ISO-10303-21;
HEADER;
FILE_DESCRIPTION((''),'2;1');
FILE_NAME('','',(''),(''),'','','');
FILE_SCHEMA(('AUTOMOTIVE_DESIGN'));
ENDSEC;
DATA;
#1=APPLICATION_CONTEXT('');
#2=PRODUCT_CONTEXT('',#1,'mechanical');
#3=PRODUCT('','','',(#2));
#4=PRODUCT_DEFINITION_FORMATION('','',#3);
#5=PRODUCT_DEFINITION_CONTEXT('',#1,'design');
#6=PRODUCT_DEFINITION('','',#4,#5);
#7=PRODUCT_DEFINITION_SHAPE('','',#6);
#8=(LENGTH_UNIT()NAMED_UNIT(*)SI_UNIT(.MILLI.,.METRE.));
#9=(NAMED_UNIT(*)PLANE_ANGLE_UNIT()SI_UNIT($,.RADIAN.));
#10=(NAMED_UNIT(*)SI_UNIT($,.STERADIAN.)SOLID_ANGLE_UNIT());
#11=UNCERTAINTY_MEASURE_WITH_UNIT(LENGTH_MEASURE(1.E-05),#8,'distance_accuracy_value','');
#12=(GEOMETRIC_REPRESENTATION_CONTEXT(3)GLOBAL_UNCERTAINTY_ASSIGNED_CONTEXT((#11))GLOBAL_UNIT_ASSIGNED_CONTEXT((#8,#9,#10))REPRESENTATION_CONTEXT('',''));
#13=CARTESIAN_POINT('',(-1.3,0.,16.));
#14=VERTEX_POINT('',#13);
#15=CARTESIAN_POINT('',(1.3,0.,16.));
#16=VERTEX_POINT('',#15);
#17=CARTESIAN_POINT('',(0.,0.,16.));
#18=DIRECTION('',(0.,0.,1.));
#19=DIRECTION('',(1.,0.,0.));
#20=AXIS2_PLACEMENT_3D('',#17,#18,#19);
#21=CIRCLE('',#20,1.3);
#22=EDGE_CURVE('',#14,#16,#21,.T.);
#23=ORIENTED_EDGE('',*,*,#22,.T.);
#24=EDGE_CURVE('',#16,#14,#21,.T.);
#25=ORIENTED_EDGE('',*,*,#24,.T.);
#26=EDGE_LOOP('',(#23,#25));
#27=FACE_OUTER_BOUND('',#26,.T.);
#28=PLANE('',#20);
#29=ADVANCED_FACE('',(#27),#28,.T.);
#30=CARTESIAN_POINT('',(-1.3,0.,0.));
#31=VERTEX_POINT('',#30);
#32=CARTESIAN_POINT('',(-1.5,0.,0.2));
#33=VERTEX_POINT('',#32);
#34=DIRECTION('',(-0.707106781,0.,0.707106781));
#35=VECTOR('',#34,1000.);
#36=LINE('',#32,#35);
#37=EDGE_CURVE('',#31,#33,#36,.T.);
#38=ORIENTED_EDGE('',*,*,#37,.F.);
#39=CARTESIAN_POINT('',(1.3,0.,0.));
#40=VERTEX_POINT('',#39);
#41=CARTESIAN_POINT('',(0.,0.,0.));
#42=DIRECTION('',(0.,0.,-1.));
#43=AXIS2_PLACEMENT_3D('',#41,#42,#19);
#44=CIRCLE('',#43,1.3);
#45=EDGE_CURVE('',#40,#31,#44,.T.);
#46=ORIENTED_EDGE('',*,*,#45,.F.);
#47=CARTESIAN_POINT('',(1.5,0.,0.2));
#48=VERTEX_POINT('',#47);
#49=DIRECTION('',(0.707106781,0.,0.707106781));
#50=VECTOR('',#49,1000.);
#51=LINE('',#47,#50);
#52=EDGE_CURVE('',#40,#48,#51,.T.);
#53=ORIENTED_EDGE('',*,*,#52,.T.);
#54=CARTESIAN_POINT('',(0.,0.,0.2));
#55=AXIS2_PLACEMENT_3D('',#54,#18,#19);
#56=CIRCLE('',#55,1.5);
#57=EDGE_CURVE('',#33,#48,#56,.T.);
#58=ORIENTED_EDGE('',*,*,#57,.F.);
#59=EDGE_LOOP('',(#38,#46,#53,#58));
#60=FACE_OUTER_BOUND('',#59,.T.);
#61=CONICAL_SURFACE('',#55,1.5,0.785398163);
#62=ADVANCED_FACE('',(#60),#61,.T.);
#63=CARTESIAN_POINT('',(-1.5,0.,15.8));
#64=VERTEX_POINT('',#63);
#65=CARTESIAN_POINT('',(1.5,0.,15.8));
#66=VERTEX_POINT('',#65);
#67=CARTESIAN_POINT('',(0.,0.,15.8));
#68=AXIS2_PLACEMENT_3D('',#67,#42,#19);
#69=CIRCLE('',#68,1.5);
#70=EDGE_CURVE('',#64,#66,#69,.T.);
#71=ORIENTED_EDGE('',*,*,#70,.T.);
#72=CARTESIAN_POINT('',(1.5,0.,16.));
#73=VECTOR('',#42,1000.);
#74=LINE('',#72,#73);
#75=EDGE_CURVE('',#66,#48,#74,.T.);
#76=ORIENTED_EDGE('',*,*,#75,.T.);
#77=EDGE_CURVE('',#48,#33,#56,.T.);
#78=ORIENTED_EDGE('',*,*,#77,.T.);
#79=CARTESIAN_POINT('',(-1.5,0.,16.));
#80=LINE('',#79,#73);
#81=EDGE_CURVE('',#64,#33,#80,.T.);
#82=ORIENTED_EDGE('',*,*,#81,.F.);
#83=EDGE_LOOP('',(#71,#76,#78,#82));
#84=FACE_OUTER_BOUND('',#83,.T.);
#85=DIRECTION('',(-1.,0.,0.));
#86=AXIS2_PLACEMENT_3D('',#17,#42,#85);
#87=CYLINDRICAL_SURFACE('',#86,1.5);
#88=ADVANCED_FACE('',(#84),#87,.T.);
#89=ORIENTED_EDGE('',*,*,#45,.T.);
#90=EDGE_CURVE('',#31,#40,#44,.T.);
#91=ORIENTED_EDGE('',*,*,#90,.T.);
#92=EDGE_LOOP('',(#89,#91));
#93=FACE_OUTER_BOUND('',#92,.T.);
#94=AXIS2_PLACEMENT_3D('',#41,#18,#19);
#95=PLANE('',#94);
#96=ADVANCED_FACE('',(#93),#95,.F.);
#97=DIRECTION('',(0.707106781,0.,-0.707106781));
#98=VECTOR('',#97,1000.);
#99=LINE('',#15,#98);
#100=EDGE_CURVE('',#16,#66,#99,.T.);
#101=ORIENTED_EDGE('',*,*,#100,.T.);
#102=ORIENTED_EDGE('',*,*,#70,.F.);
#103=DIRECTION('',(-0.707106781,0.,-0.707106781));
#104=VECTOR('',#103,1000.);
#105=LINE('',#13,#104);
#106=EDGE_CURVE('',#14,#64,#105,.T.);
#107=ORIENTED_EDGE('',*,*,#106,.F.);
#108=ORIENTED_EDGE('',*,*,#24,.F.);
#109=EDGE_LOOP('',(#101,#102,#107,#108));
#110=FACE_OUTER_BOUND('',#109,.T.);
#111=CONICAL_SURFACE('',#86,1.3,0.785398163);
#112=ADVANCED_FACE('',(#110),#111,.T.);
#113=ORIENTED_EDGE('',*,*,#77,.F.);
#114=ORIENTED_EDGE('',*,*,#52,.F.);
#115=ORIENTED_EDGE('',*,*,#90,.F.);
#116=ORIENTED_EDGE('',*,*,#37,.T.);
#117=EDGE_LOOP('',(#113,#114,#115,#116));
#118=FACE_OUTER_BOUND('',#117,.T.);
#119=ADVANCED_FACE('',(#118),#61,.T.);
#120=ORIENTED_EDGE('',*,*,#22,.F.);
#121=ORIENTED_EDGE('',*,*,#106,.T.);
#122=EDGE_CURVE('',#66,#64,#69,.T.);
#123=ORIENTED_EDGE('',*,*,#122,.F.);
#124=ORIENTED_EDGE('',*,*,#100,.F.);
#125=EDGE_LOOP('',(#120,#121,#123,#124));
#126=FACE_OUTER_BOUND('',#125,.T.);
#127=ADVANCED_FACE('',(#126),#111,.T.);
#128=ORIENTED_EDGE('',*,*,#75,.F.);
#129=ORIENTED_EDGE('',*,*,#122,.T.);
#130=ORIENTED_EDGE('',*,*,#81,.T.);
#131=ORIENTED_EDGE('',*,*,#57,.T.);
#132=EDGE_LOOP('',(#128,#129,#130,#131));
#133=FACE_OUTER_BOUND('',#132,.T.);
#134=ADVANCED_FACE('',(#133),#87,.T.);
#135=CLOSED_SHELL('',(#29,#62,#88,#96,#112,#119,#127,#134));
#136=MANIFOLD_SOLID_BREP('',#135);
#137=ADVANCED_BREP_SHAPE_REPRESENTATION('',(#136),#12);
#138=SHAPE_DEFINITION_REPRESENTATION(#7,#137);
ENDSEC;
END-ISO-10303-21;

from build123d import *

# Parameters (mm, degrees)
SKETCH1_R           = 1.5
BOSS_EXTRUDE1_DEPTH = 16
CHAMFER1_SIZE       = 0.2


with BuildPart() as part:
    # Sketch1 → Boss-Extrude1 (new body)
    with BuildSketch(Plane.XY):
        Circle(SKETCH1_R)
    extrude(amount=BOSS_EXTRUDE1_DEPTH)

    # Chamfer1
    chamfer1_edges = [part.edges().sort_by_distance(p)[0] for p in [
        (-1.5, 0, 0),
        (-1.5, 0, 16),
    ]]
    chamfer(chamfer1_edges, length=CHAMFER1_SIZE)


solid = part.part
